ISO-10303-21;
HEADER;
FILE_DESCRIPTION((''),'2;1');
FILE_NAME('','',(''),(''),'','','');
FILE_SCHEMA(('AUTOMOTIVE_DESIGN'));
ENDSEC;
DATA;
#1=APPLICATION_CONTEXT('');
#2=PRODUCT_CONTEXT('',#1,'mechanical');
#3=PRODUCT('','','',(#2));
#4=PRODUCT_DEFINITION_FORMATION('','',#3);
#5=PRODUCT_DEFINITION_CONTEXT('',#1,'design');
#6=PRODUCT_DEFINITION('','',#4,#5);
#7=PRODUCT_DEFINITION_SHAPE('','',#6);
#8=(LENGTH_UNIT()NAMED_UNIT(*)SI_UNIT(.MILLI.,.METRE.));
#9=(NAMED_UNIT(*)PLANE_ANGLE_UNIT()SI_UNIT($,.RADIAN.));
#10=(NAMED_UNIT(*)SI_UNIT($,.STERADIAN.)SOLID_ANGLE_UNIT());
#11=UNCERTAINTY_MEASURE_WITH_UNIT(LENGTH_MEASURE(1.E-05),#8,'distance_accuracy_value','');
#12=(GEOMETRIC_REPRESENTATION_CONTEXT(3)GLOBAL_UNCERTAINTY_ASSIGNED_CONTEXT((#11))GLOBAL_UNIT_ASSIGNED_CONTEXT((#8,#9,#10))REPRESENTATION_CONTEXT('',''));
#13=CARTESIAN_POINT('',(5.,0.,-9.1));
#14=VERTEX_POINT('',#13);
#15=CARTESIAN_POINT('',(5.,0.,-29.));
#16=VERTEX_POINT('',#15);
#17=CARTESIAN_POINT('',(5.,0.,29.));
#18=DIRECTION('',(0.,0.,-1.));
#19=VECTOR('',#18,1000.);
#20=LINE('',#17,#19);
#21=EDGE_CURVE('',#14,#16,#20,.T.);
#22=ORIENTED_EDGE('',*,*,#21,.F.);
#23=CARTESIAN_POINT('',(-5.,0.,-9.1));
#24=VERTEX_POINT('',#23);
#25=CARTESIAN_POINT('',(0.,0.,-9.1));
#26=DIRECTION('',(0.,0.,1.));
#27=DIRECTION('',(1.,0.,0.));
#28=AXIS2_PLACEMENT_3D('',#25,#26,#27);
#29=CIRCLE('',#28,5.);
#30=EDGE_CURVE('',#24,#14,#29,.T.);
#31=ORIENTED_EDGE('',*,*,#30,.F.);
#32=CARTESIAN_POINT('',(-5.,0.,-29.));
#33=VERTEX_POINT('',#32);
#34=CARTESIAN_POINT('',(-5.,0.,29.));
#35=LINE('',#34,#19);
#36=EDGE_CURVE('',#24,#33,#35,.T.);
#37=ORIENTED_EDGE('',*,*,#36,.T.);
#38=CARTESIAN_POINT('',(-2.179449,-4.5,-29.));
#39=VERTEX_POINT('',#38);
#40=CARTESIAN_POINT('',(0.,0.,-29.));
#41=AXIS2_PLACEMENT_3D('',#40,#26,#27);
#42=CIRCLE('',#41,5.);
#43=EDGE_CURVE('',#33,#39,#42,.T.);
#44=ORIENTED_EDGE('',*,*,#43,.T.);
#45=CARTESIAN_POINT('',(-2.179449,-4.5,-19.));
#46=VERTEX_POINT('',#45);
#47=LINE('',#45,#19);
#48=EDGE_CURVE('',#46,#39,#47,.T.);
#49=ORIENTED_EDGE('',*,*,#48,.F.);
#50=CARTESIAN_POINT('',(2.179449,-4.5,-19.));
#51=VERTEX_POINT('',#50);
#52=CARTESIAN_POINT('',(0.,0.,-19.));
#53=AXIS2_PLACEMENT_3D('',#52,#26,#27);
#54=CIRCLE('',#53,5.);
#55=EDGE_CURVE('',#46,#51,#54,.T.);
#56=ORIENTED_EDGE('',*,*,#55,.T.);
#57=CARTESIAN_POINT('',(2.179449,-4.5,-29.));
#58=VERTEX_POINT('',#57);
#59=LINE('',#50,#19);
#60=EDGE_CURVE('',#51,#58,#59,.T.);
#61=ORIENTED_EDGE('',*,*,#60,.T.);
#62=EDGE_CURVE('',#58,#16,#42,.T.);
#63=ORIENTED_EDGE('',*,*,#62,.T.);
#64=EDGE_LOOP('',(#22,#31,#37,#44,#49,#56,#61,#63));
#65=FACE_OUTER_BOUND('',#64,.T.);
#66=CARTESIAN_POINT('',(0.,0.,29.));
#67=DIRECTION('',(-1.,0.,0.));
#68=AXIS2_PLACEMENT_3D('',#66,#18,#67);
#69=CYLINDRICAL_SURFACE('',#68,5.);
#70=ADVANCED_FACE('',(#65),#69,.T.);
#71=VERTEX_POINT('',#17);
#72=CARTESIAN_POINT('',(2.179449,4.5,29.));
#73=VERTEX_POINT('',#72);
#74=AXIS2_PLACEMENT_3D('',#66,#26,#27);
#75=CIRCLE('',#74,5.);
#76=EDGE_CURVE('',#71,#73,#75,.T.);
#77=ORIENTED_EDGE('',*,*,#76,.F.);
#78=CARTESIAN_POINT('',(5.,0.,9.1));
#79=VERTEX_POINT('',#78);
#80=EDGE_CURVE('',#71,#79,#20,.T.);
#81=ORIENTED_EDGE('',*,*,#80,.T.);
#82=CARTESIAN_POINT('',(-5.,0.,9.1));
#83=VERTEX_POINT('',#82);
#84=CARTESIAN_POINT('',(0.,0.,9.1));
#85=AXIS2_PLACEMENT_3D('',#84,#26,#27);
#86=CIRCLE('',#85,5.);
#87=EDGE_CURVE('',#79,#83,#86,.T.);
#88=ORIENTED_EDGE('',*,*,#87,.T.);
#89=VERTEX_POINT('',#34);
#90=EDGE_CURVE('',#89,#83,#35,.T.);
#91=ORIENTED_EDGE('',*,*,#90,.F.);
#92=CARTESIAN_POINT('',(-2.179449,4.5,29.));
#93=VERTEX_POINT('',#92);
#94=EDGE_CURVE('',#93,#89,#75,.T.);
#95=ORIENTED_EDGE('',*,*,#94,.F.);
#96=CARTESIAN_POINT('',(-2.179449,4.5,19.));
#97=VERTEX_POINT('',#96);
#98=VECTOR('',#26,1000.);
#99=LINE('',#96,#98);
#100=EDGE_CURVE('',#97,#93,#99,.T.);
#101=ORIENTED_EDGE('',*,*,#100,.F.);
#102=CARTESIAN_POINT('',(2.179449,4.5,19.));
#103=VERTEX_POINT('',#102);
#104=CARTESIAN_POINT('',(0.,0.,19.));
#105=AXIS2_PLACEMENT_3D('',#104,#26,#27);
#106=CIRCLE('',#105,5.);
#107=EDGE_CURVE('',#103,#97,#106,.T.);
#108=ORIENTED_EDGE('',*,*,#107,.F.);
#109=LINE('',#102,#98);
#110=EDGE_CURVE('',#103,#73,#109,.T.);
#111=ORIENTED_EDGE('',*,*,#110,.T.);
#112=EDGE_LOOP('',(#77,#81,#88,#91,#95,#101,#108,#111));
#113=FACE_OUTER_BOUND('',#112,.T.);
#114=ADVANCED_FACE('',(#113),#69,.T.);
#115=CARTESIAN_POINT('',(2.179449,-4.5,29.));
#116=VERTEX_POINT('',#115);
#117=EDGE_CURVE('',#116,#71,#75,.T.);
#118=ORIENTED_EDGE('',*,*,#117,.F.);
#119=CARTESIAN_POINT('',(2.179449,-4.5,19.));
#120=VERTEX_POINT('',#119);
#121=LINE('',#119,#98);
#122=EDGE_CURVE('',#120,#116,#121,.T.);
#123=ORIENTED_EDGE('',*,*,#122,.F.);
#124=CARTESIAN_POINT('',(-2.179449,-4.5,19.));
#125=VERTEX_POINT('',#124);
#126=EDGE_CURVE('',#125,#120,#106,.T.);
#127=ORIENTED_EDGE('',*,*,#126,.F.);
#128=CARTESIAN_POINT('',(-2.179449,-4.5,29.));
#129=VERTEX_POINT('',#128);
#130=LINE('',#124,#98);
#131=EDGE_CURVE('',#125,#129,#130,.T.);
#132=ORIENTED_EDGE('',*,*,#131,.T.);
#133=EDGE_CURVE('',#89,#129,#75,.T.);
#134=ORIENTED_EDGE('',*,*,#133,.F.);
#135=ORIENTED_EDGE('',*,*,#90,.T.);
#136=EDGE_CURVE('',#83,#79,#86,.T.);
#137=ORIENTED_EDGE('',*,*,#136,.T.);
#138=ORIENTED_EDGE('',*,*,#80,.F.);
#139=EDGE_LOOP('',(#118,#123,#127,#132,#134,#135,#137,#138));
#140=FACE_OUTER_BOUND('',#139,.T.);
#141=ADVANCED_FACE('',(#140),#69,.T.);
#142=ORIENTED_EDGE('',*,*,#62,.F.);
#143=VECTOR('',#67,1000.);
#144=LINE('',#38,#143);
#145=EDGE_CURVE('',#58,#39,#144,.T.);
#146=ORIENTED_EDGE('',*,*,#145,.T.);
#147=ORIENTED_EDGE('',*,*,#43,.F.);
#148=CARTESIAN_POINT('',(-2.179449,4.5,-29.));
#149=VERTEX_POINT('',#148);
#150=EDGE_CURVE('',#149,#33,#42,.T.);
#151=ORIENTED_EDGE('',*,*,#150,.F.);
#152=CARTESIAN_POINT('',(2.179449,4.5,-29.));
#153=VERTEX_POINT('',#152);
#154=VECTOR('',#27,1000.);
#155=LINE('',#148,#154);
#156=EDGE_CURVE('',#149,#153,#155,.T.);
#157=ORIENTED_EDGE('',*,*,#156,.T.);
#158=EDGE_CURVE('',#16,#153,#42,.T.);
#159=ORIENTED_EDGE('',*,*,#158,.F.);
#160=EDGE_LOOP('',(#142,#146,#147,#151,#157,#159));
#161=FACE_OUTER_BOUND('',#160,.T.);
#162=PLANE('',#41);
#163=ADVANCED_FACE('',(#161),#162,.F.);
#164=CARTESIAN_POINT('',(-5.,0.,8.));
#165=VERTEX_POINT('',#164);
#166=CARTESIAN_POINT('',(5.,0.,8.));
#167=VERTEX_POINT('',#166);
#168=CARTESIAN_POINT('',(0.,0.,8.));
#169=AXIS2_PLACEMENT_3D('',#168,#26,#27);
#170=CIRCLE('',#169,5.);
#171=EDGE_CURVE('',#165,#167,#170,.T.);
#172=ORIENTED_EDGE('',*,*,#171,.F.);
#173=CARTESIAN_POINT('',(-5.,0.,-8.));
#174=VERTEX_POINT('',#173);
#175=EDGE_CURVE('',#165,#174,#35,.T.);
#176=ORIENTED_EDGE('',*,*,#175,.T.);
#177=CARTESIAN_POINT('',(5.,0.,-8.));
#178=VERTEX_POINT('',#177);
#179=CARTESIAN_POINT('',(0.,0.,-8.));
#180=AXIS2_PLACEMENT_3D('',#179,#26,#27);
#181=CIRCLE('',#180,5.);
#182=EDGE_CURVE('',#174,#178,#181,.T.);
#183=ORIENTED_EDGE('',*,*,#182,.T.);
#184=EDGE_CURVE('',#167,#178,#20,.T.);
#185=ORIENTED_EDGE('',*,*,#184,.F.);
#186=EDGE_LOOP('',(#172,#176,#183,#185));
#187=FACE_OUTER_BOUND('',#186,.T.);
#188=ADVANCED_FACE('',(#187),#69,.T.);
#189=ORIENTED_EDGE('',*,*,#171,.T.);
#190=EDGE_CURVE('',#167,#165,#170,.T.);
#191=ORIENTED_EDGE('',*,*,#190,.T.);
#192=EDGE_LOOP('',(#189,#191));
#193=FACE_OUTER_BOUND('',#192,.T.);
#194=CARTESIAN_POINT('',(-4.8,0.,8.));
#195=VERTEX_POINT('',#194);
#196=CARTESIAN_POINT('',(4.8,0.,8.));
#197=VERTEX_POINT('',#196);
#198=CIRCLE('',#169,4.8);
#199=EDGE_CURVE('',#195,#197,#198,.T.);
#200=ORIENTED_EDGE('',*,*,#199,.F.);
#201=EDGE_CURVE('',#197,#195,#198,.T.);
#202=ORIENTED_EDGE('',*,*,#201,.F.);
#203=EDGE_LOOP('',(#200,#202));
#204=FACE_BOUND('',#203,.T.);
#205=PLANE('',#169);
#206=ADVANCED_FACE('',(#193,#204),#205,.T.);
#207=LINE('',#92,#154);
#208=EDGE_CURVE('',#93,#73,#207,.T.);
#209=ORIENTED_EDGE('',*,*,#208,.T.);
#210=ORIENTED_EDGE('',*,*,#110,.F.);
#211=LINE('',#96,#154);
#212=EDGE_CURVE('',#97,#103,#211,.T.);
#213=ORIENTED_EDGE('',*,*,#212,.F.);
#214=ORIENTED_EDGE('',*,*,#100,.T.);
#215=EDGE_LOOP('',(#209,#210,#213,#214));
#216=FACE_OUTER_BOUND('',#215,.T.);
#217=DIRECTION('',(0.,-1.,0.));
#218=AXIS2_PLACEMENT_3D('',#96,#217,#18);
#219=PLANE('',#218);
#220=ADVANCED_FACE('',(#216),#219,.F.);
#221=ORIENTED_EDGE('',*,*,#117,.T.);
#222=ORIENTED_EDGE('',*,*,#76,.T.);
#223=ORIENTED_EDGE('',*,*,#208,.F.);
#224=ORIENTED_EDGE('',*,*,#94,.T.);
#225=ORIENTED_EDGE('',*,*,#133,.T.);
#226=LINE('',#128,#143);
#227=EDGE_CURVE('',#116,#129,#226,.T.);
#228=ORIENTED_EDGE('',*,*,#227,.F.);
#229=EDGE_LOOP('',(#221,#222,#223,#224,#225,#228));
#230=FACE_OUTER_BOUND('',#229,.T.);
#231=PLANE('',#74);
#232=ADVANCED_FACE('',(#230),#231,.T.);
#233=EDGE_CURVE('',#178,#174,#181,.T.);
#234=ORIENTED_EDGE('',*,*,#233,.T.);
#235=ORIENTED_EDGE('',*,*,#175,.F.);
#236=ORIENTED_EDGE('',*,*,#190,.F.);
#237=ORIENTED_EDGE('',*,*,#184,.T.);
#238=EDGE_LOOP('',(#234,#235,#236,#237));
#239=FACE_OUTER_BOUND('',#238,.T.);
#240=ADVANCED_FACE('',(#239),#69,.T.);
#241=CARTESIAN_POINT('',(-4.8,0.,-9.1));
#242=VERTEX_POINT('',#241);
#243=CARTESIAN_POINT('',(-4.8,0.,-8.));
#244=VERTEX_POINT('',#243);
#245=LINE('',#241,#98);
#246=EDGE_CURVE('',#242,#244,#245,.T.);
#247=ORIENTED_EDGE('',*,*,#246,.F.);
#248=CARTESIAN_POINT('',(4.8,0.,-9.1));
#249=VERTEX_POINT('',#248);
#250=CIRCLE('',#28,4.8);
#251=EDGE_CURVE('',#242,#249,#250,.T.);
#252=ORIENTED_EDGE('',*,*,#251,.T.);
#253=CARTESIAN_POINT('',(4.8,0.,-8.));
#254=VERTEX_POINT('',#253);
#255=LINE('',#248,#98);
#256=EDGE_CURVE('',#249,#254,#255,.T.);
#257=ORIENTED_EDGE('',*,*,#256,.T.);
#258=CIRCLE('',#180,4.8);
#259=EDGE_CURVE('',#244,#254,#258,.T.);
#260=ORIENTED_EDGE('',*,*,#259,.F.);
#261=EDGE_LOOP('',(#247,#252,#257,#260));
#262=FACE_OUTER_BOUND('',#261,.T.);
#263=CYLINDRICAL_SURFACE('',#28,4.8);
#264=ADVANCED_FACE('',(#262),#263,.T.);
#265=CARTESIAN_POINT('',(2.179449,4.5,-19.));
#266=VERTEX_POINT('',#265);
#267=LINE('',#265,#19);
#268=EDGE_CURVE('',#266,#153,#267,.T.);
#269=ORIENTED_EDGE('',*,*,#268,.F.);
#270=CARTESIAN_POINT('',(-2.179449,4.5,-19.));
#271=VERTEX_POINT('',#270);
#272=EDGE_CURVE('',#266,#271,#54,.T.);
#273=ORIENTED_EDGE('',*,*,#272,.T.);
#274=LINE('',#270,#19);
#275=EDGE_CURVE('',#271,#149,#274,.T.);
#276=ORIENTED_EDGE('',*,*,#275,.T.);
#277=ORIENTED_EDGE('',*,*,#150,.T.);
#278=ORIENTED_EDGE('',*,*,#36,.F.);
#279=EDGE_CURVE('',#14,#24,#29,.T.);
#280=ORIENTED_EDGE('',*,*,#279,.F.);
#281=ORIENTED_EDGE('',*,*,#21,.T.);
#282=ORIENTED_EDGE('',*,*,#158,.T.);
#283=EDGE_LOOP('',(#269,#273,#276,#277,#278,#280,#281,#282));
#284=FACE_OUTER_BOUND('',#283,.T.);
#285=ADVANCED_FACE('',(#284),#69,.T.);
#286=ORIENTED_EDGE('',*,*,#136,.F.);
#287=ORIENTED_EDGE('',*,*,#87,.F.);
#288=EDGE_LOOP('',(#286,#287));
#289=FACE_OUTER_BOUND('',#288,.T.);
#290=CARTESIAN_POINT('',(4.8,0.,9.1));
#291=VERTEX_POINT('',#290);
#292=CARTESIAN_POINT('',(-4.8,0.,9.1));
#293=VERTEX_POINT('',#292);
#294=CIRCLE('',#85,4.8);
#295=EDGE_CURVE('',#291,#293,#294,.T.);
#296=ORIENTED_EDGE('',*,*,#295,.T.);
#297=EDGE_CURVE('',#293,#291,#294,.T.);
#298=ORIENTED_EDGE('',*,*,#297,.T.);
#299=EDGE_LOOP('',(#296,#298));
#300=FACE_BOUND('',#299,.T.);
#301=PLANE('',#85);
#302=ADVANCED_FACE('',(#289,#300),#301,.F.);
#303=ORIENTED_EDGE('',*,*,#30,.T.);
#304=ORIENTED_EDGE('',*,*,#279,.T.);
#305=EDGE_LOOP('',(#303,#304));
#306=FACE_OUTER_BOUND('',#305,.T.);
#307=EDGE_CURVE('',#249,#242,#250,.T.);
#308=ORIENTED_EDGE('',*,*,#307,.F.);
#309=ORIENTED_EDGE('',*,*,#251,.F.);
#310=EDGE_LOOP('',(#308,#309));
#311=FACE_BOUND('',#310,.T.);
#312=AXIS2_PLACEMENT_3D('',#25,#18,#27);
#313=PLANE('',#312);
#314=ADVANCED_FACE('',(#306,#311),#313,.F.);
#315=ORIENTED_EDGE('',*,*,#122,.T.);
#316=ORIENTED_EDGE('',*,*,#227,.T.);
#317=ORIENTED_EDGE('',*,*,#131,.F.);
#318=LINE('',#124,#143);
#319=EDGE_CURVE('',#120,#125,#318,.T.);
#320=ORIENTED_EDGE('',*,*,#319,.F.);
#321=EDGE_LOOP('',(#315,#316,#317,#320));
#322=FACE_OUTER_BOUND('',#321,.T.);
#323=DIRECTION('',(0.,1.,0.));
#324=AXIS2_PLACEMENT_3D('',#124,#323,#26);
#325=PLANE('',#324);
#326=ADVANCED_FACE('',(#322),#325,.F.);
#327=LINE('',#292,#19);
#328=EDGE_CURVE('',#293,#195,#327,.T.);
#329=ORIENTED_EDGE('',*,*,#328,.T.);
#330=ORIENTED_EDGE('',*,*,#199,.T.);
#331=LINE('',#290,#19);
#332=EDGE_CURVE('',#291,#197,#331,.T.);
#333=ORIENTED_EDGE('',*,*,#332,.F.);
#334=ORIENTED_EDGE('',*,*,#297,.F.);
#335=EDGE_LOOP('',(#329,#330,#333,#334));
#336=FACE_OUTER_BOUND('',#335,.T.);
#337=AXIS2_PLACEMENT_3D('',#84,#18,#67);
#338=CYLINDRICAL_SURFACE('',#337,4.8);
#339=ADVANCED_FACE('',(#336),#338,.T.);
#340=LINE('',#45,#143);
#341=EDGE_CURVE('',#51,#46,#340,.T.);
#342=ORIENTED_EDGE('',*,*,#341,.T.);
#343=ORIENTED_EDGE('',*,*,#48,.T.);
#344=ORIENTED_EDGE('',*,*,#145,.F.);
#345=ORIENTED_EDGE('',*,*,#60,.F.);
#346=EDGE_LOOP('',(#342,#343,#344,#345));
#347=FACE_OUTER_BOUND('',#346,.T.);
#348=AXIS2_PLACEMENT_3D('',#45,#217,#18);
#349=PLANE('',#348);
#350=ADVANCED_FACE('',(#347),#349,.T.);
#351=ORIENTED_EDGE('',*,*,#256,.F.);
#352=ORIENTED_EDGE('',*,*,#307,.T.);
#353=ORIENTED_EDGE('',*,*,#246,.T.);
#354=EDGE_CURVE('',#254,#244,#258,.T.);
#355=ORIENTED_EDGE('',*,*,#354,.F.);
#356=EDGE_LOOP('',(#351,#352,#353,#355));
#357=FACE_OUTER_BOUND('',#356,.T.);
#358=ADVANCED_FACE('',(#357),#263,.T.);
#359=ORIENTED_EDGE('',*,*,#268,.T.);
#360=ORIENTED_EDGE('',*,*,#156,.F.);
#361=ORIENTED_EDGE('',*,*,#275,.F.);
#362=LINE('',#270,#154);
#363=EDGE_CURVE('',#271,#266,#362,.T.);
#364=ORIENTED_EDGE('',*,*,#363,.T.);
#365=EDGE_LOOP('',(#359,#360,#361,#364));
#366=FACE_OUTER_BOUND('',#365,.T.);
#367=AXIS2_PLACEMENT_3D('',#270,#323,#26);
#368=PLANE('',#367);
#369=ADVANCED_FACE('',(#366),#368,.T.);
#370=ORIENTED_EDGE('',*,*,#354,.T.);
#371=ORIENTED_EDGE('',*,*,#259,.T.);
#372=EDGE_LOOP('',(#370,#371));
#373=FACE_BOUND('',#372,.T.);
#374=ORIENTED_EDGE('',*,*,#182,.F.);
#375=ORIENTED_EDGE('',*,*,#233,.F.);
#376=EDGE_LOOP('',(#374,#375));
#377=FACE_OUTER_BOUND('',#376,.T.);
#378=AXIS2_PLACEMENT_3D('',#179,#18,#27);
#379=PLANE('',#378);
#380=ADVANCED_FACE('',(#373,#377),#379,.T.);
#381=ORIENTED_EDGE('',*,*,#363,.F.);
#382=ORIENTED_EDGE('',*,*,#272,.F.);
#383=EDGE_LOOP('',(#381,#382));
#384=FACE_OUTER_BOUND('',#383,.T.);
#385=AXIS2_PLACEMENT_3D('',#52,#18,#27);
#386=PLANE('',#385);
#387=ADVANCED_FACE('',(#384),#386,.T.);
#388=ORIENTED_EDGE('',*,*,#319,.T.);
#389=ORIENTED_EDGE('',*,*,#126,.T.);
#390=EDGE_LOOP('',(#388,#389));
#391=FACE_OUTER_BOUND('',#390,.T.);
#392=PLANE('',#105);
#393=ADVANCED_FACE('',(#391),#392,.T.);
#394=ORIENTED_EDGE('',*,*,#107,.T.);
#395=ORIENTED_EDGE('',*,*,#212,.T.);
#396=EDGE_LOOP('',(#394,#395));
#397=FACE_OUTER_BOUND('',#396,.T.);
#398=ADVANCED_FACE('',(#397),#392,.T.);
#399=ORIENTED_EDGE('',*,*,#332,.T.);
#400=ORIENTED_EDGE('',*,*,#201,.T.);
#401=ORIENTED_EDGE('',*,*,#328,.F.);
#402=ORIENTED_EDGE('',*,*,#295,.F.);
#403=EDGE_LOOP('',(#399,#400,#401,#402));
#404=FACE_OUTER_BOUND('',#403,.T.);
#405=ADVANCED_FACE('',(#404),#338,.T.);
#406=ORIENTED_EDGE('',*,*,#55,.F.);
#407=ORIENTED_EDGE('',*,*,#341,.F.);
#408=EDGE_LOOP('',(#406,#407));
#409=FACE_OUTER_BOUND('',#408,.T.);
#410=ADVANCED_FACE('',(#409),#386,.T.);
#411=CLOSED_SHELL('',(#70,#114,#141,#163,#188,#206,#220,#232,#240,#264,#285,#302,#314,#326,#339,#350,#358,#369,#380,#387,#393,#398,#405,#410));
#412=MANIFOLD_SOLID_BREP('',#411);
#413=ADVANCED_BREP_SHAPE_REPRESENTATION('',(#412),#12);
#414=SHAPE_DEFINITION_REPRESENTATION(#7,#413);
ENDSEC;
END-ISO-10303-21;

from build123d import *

# Parameters (mm, degrees)
SKETCH_1_R          = 5
EXTRUDE_1_DEPTH     = 29
CUT_EXTRUDE_START   = 1.1
SKETCH_3_R          = 5
SKETCH_3_R_2        = 4.8
CUT_EXTRUDE_2_DEPTH = 1.1
CUT_EXTRUDE_1_DEPTH = 10


with BuildPart() as part:
    # 草图1 → 凸台-拉伸1 (new, symmetric)
    with BuildSketch(Plane.XY):
        with Locations(Location((0, 0, 0), (0, 0, 180))):
            Circle(SKETCH_1_R)
    extrude(amount=EXTRUDE_1_DEPTH, both=True)

    # 草图3 → 切除-拉伸2 (cut)
    with BuildSketch(Plane.XY.offset(8).offset(CUT_EXTRUDE_START)):
        with Locations(Location((0, 0, 0), (0, 0, 180))):
            Circle(SKETCH_3_R)
        Circle(SKETCH_3_R_2, mode=Mode.SUBTRACT)
    cut_extrude_2 = extrude(amount=-CUT_EXTRUDE_2_DEPTH, mode=Mode.SUBTRACT)

    # 镜向2: 切除-拉伸2 across plane
    add(cut_extrude_2.mirror(Plane.XY), mode=Mode.SUBTRACT)

    # 草图2 → 切除-拉伸1 (cut)
    with BuildSketch(Plane.XY.offset(29)):
        with BuildLine():
            Line((-2.179449472, 4.5), (2.179449472, 4.5))
            ThreePointArc((2.179449472, 4.5), (0, 5), (-2.179449472, 4.5))
        make_face()
        with BuildLine():
            Line((-2.179449472, -4.5), (2.179449472, -4.5))
            ThreePointArc((2.179449472, -4.5), (0, -5), (-2.179449472, -4.5))
        make_face()
    cut_extrude_1 = extrude(amount=-CUT_EXTRUDE_1_DEPTH, mode=Mode.SUBTRACT)

    # 镜向1: 切除-拉伸1 across plane
    add(cut_extrude_1.mirror(Plane.XY), mode=Mode.SUBTRACT)


solid = part.part
